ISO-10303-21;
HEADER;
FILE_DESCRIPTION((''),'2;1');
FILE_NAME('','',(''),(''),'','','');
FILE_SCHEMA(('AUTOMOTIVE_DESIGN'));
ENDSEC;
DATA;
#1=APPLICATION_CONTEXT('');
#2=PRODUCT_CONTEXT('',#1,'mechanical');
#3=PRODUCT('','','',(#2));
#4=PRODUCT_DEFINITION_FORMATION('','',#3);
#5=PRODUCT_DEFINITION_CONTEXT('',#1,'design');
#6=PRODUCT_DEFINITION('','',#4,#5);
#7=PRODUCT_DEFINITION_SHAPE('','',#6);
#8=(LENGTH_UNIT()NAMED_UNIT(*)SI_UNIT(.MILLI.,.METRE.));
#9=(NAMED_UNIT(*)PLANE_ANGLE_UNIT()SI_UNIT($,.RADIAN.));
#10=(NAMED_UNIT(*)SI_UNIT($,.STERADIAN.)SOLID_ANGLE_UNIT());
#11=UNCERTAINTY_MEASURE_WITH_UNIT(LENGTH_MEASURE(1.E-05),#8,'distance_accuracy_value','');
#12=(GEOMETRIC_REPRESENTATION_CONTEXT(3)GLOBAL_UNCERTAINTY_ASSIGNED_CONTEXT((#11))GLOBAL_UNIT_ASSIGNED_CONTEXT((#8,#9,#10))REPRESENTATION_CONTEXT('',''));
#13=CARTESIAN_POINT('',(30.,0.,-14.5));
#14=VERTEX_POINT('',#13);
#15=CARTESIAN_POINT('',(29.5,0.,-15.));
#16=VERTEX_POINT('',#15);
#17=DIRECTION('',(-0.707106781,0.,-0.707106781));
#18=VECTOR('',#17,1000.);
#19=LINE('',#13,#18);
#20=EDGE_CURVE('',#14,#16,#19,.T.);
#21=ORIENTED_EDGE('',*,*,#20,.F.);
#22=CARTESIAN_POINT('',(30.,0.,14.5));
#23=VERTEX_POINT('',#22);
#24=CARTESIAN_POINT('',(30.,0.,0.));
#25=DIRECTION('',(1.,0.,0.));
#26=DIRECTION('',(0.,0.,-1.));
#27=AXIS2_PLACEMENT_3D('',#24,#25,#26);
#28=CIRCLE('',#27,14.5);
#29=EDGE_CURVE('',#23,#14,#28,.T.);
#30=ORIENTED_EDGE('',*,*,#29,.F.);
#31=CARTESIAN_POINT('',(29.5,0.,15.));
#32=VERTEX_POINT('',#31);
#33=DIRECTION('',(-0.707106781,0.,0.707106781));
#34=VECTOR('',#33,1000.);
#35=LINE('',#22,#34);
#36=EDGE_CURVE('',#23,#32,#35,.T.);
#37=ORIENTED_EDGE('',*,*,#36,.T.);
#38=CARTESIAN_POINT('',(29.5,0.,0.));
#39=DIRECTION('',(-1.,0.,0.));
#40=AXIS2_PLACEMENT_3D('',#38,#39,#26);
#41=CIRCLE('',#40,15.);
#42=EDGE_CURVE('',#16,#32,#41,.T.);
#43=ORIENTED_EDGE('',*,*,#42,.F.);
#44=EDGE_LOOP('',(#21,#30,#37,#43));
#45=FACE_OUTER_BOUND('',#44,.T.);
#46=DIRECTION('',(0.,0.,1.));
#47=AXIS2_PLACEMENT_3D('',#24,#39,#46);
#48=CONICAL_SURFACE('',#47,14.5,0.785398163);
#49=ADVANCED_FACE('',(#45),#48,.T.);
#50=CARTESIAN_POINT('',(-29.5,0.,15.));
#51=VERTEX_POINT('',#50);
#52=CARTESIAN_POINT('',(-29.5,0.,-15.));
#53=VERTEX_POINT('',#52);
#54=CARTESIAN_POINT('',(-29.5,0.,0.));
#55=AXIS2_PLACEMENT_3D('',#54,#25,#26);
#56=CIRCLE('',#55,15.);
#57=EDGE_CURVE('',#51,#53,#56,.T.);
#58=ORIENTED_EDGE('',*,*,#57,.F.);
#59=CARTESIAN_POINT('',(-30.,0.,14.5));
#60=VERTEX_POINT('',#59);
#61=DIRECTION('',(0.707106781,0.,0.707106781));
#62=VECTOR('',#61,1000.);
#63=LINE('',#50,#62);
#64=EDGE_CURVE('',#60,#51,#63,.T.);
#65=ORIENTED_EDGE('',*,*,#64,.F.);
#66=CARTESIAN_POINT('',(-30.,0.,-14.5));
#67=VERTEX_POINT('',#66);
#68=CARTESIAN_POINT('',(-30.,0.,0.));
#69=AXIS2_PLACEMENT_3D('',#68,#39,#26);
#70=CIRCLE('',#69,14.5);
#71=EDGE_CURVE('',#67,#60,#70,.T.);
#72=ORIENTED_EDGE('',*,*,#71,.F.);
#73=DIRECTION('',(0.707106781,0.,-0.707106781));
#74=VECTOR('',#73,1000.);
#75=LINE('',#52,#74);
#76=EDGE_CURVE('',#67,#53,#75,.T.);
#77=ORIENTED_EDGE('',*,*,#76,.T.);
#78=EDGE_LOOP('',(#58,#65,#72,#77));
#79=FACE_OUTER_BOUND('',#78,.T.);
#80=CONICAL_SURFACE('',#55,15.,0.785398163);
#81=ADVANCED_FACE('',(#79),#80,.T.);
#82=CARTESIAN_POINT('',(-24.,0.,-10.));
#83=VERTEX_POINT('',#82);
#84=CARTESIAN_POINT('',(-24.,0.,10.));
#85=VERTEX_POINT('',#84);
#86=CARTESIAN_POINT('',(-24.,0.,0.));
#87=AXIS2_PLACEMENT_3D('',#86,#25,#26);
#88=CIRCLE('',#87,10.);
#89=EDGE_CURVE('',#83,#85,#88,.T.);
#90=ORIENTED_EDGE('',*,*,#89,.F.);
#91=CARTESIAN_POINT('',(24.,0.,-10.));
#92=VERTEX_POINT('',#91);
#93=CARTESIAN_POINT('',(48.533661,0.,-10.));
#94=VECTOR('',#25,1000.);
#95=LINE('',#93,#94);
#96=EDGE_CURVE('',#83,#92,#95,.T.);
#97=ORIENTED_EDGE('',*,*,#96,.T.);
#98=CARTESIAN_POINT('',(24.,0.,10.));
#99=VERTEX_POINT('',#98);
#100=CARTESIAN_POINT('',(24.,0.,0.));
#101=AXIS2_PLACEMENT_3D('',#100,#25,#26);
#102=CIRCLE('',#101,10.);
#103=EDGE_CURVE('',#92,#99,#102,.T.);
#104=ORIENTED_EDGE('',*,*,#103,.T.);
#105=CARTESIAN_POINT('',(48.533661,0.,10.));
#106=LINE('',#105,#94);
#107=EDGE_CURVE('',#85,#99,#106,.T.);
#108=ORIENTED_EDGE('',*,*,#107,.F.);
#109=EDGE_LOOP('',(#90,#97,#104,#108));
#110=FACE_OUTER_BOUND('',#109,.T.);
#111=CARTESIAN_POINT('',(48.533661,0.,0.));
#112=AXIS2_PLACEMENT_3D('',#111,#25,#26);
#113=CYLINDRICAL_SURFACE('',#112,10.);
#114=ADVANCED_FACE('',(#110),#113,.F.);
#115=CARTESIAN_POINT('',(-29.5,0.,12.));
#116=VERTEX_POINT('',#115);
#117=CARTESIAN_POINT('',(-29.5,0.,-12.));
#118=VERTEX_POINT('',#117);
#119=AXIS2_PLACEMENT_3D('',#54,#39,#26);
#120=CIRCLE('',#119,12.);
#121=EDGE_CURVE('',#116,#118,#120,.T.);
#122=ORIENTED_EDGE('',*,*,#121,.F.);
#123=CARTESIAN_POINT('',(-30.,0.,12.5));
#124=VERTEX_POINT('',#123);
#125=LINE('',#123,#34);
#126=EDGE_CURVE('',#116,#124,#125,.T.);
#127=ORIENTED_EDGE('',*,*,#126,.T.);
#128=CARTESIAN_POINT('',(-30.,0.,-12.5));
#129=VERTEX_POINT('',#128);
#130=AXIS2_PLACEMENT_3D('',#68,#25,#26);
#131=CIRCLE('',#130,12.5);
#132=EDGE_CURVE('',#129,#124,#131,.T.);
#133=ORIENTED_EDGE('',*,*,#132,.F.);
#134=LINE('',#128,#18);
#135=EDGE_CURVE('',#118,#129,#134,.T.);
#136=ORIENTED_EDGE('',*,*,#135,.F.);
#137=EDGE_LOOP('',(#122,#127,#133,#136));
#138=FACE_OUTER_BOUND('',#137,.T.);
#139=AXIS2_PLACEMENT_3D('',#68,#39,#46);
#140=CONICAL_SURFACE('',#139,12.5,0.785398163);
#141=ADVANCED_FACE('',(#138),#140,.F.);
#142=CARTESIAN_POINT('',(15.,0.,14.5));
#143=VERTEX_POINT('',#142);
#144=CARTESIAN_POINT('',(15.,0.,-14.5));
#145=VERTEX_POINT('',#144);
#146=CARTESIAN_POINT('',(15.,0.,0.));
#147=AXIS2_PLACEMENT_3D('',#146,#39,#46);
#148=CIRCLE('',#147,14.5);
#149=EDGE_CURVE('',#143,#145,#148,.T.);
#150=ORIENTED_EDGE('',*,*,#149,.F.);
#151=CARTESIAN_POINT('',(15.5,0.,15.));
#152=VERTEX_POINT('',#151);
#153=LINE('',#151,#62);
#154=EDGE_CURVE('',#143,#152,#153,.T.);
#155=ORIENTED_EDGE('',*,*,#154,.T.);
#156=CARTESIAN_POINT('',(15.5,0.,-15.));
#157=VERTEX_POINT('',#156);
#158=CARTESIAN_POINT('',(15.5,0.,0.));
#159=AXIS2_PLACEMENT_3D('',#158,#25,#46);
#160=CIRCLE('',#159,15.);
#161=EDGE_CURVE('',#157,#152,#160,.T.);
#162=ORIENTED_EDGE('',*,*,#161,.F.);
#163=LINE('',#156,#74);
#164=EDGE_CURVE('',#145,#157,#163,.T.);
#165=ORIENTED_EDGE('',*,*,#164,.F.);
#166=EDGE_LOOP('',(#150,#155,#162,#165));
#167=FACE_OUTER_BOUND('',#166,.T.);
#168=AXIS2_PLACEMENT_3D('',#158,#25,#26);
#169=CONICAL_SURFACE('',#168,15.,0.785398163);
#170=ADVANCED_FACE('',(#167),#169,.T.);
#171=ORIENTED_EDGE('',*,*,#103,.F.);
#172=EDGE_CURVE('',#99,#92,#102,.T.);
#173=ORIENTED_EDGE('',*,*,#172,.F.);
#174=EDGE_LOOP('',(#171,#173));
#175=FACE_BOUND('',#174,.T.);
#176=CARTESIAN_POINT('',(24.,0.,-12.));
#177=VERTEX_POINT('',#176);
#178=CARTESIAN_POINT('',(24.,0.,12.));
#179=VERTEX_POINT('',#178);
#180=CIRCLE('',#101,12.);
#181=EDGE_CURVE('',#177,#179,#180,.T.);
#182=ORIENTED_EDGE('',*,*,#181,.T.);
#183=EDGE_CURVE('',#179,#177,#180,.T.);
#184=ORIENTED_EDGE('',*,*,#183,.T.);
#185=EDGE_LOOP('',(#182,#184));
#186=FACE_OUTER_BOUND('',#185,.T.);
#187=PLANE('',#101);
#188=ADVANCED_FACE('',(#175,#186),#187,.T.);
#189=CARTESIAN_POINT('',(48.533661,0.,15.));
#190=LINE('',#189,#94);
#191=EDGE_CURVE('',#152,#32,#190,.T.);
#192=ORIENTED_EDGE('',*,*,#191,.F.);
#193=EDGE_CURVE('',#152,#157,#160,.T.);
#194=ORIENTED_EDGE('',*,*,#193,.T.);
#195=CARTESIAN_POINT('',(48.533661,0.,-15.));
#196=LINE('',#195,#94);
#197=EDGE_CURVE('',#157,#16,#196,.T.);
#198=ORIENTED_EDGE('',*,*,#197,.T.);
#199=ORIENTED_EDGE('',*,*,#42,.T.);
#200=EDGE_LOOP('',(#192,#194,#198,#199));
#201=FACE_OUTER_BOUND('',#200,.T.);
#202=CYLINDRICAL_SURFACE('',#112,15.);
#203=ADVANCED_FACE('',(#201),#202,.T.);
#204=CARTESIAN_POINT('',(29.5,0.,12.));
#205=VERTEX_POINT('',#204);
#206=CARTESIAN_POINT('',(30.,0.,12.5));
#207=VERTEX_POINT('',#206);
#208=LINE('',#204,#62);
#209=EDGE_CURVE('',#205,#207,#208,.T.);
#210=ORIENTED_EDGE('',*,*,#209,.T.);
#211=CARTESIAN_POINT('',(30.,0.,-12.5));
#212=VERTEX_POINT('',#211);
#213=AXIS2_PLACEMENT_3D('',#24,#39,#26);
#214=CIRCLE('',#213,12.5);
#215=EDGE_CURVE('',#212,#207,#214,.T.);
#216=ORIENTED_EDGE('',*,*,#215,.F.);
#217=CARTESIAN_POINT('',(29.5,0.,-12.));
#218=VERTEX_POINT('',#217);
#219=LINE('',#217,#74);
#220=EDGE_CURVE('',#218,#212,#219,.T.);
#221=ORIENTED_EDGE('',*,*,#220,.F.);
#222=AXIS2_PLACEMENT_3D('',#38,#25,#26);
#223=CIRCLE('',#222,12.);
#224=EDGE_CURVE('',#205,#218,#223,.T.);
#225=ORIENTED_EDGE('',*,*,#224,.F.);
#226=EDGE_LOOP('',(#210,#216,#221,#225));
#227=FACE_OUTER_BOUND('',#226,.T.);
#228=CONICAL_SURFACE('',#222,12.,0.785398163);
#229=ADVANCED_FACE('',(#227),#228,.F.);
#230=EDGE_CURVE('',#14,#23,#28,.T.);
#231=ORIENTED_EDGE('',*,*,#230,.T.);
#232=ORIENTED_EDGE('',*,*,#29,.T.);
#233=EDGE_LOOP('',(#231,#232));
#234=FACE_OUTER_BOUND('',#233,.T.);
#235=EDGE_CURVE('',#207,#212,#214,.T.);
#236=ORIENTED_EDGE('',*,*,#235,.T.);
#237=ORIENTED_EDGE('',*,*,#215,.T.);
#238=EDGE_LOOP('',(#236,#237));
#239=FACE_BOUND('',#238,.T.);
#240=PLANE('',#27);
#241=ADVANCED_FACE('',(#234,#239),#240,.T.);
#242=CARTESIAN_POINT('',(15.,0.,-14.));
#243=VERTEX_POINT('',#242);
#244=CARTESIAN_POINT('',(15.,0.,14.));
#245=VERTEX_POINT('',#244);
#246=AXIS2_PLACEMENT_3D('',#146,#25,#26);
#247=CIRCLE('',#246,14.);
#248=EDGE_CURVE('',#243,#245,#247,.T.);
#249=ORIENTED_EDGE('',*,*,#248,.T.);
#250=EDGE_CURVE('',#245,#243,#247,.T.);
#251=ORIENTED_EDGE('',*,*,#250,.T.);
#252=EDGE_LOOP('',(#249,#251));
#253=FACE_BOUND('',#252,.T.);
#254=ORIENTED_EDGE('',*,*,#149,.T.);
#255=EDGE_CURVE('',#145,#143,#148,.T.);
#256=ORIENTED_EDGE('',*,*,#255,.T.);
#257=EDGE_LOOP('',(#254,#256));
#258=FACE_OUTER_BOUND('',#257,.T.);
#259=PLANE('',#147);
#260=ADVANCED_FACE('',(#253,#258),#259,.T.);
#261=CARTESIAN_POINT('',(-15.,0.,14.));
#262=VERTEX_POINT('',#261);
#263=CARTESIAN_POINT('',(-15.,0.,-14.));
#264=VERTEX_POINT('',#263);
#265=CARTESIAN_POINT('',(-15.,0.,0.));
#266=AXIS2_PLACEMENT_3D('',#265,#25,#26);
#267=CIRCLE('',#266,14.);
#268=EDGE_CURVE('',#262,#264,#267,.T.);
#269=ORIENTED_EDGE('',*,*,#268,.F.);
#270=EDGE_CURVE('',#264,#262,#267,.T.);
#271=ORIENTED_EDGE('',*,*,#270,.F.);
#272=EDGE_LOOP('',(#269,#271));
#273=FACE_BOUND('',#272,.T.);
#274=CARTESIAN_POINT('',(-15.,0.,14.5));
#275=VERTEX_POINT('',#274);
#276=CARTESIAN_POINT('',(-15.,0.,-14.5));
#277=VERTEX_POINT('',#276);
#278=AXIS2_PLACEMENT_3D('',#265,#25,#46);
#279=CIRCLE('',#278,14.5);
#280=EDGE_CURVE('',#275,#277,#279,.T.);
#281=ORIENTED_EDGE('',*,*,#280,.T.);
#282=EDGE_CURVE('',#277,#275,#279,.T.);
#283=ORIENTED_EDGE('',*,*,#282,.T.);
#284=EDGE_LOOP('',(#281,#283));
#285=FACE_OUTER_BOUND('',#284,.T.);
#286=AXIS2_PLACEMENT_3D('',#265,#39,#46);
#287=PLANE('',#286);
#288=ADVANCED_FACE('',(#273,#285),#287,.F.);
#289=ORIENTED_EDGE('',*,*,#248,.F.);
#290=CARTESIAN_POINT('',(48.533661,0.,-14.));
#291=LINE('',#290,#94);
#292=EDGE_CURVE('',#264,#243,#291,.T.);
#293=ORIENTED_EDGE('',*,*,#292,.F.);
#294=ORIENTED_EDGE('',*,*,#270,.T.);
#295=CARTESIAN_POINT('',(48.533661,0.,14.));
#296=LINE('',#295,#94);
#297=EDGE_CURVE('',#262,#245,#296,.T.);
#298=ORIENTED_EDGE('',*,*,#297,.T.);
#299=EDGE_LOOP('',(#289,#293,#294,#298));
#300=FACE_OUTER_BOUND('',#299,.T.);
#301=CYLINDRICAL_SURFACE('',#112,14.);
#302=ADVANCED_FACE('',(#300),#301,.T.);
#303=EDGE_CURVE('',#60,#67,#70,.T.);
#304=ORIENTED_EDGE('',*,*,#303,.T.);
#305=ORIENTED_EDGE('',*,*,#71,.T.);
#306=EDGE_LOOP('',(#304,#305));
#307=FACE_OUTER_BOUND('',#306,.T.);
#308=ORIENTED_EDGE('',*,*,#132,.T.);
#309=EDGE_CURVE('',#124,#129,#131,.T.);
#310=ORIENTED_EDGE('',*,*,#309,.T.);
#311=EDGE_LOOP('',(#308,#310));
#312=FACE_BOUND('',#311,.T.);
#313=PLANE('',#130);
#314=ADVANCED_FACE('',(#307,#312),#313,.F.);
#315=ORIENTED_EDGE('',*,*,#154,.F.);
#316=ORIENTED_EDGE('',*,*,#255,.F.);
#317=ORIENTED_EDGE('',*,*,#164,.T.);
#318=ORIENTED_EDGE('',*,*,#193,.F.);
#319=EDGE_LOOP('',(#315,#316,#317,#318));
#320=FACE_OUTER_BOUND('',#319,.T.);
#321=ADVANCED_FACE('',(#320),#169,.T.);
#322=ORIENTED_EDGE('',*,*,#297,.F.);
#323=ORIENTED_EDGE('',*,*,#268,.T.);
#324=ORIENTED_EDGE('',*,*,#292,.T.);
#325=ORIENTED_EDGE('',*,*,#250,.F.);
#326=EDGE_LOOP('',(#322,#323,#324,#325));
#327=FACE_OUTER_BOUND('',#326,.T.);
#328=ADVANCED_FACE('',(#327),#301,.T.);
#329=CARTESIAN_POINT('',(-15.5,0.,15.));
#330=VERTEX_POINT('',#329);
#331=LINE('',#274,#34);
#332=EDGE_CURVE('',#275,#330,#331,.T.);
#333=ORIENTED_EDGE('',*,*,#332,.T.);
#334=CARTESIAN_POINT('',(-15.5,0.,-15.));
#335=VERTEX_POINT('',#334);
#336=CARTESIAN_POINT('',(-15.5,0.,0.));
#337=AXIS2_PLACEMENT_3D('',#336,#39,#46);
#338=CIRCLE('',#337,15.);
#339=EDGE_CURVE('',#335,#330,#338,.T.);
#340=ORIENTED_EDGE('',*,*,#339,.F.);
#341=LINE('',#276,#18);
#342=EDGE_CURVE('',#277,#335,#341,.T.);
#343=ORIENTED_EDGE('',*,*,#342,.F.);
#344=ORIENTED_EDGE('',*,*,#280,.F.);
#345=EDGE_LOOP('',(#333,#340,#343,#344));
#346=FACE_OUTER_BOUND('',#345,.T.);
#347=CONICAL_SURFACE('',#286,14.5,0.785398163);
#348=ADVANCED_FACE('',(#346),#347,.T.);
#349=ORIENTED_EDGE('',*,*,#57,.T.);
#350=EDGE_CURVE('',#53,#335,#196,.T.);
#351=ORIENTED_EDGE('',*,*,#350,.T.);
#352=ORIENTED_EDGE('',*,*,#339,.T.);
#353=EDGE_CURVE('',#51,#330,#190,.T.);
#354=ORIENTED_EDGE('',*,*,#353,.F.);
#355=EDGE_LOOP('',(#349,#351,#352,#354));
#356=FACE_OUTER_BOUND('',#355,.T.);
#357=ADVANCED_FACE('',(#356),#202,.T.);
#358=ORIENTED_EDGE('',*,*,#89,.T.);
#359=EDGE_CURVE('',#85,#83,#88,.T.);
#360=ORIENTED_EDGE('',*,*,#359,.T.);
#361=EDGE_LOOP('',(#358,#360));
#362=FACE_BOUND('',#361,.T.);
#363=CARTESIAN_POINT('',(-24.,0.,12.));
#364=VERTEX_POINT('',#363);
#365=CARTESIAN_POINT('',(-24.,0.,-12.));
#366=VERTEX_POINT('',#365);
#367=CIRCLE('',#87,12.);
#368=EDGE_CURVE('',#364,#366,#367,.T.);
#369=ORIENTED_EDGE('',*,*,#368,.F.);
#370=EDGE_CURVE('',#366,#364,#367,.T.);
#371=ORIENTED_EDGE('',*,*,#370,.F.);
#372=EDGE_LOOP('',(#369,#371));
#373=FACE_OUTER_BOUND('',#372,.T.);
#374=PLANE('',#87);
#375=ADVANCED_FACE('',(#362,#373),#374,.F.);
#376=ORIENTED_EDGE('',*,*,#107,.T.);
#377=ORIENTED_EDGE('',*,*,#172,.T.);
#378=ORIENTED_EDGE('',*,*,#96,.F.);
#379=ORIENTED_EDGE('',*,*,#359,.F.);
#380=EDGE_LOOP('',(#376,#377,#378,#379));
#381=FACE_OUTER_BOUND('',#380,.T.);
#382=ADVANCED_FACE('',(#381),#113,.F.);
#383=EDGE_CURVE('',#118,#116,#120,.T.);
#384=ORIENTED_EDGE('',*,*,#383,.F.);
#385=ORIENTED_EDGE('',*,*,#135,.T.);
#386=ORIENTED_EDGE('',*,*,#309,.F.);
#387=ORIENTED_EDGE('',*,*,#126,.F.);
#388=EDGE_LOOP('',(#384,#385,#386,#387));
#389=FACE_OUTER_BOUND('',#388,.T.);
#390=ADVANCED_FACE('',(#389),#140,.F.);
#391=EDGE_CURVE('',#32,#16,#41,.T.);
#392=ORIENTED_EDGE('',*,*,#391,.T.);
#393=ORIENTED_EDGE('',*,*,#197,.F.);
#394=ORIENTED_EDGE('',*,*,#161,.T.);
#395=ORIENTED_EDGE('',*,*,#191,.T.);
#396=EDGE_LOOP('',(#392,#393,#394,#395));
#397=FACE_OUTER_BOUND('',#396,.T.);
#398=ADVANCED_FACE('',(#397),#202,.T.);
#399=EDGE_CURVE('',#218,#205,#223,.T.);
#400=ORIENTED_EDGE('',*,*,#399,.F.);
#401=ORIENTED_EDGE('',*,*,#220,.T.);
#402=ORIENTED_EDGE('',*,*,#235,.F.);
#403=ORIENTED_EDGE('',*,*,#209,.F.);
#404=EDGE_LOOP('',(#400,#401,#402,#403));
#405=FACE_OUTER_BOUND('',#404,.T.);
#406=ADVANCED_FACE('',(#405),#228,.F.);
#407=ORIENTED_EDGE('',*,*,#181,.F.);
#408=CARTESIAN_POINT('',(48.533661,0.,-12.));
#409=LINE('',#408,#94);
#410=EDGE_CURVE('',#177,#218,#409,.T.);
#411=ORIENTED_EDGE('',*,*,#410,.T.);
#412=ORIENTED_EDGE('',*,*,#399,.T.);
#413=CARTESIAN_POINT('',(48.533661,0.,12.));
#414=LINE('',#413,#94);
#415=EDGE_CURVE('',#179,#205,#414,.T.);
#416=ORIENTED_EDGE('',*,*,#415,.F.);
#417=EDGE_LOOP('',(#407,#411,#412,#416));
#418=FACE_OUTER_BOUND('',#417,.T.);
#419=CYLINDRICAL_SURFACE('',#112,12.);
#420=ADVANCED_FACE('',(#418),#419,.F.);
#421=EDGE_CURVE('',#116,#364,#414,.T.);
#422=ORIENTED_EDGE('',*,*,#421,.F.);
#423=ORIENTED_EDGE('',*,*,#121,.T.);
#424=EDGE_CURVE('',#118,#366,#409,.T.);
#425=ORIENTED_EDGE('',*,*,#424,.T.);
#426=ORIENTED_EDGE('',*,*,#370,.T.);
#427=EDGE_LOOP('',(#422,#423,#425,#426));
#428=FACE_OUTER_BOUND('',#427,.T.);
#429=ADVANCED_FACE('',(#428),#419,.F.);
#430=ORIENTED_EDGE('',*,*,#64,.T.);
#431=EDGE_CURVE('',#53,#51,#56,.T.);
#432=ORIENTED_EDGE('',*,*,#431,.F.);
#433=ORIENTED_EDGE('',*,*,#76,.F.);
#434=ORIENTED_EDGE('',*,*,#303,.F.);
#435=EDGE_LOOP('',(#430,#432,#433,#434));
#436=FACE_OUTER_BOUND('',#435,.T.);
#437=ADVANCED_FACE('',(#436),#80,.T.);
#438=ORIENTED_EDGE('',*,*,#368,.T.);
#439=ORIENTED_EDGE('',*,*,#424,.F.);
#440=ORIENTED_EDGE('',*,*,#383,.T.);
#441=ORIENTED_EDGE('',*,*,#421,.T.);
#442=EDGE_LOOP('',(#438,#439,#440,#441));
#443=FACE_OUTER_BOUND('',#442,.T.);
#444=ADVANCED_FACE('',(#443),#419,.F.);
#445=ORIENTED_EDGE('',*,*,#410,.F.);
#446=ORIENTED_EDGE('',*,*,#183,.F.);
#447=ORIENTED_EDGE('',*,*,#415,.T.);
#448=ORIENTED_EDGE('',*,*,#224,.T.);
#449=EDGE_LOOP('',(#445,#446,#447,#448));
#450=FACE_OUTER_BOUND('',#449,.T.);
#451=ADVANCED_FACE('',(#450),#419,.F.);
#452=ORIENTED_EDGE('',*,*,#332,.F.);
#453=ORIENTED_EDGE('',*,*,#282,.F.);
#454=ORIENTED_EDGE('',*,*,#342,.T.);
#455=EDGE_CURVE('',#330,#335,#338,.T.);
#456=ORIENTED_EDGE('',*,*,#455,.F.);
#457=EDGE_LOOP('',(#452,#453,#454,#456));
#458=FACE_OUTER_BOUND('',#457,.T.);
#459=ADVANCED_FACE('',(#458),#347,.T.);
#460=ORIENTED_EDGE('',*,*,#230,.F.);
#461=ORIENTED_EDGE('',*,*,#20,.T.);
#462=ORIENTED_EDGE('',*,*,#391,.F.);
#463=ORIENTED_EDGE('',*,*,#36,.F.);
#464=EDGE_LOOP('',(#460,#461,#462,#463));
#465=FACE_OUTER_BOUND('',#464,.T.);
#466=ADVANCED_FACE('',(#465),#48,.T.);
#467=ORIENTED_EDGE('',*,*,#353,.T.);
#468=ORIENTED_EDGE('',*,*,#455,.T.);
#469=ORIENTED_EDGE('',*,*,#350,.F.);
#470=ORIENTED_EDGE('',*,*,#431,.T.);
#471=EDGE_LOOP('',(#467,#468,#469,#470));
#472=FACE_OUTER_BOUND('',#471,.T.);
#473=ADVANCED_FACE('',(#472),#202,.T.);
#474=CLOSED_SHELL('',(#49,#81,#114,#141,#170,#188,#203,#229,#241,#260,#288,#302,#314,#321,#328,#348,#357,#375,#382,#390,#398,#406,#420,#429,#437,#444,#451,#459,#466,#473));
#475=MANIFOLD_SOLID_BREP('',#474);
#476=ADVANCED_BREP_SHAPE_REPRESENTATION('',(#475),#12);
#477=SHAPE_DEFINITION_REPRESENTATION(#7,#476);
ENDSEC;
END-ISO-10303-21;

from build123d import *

# Parameters (mm, degrees)
CHAMFER1_SIZE = 0.5


with BuildPart() as part:
    # Sketch1 → Revolve1 (revolve)
    with BuildSketch(Plane.XY, mode=Mode.PRIVATE) as revolve1_sk:
        Polygon((-24, 12), (-24, 10), (24, 10), (24, 12), (30, 12), (30, 15), (15, 15), (15, 14), (-15, 14), (-15, 15), (-30, 15), (-30, 12), align=None)
    revolve(revolve1_sk.sketch.rotate(Axis((48.533661203, 0, 0), (-1, 0, 0)), 90), axis=Axis((48.533661203, 0, 0), (-1, 0, 0)))

    # Chamfer1
    chamfer1_edges = [part.edges().sort_by_distance(p)[0] for p in [
        (30, 0, 12),
        (-30, 0, 12),
        (-30, 0, 15),
        (-15, 0, 15),
        (15, 0, 15),
        (30, 0, 15),
    ]]
    chamfer(chamfer1_edges, length=CHAMFER1_SIZE)


solid = part.part
